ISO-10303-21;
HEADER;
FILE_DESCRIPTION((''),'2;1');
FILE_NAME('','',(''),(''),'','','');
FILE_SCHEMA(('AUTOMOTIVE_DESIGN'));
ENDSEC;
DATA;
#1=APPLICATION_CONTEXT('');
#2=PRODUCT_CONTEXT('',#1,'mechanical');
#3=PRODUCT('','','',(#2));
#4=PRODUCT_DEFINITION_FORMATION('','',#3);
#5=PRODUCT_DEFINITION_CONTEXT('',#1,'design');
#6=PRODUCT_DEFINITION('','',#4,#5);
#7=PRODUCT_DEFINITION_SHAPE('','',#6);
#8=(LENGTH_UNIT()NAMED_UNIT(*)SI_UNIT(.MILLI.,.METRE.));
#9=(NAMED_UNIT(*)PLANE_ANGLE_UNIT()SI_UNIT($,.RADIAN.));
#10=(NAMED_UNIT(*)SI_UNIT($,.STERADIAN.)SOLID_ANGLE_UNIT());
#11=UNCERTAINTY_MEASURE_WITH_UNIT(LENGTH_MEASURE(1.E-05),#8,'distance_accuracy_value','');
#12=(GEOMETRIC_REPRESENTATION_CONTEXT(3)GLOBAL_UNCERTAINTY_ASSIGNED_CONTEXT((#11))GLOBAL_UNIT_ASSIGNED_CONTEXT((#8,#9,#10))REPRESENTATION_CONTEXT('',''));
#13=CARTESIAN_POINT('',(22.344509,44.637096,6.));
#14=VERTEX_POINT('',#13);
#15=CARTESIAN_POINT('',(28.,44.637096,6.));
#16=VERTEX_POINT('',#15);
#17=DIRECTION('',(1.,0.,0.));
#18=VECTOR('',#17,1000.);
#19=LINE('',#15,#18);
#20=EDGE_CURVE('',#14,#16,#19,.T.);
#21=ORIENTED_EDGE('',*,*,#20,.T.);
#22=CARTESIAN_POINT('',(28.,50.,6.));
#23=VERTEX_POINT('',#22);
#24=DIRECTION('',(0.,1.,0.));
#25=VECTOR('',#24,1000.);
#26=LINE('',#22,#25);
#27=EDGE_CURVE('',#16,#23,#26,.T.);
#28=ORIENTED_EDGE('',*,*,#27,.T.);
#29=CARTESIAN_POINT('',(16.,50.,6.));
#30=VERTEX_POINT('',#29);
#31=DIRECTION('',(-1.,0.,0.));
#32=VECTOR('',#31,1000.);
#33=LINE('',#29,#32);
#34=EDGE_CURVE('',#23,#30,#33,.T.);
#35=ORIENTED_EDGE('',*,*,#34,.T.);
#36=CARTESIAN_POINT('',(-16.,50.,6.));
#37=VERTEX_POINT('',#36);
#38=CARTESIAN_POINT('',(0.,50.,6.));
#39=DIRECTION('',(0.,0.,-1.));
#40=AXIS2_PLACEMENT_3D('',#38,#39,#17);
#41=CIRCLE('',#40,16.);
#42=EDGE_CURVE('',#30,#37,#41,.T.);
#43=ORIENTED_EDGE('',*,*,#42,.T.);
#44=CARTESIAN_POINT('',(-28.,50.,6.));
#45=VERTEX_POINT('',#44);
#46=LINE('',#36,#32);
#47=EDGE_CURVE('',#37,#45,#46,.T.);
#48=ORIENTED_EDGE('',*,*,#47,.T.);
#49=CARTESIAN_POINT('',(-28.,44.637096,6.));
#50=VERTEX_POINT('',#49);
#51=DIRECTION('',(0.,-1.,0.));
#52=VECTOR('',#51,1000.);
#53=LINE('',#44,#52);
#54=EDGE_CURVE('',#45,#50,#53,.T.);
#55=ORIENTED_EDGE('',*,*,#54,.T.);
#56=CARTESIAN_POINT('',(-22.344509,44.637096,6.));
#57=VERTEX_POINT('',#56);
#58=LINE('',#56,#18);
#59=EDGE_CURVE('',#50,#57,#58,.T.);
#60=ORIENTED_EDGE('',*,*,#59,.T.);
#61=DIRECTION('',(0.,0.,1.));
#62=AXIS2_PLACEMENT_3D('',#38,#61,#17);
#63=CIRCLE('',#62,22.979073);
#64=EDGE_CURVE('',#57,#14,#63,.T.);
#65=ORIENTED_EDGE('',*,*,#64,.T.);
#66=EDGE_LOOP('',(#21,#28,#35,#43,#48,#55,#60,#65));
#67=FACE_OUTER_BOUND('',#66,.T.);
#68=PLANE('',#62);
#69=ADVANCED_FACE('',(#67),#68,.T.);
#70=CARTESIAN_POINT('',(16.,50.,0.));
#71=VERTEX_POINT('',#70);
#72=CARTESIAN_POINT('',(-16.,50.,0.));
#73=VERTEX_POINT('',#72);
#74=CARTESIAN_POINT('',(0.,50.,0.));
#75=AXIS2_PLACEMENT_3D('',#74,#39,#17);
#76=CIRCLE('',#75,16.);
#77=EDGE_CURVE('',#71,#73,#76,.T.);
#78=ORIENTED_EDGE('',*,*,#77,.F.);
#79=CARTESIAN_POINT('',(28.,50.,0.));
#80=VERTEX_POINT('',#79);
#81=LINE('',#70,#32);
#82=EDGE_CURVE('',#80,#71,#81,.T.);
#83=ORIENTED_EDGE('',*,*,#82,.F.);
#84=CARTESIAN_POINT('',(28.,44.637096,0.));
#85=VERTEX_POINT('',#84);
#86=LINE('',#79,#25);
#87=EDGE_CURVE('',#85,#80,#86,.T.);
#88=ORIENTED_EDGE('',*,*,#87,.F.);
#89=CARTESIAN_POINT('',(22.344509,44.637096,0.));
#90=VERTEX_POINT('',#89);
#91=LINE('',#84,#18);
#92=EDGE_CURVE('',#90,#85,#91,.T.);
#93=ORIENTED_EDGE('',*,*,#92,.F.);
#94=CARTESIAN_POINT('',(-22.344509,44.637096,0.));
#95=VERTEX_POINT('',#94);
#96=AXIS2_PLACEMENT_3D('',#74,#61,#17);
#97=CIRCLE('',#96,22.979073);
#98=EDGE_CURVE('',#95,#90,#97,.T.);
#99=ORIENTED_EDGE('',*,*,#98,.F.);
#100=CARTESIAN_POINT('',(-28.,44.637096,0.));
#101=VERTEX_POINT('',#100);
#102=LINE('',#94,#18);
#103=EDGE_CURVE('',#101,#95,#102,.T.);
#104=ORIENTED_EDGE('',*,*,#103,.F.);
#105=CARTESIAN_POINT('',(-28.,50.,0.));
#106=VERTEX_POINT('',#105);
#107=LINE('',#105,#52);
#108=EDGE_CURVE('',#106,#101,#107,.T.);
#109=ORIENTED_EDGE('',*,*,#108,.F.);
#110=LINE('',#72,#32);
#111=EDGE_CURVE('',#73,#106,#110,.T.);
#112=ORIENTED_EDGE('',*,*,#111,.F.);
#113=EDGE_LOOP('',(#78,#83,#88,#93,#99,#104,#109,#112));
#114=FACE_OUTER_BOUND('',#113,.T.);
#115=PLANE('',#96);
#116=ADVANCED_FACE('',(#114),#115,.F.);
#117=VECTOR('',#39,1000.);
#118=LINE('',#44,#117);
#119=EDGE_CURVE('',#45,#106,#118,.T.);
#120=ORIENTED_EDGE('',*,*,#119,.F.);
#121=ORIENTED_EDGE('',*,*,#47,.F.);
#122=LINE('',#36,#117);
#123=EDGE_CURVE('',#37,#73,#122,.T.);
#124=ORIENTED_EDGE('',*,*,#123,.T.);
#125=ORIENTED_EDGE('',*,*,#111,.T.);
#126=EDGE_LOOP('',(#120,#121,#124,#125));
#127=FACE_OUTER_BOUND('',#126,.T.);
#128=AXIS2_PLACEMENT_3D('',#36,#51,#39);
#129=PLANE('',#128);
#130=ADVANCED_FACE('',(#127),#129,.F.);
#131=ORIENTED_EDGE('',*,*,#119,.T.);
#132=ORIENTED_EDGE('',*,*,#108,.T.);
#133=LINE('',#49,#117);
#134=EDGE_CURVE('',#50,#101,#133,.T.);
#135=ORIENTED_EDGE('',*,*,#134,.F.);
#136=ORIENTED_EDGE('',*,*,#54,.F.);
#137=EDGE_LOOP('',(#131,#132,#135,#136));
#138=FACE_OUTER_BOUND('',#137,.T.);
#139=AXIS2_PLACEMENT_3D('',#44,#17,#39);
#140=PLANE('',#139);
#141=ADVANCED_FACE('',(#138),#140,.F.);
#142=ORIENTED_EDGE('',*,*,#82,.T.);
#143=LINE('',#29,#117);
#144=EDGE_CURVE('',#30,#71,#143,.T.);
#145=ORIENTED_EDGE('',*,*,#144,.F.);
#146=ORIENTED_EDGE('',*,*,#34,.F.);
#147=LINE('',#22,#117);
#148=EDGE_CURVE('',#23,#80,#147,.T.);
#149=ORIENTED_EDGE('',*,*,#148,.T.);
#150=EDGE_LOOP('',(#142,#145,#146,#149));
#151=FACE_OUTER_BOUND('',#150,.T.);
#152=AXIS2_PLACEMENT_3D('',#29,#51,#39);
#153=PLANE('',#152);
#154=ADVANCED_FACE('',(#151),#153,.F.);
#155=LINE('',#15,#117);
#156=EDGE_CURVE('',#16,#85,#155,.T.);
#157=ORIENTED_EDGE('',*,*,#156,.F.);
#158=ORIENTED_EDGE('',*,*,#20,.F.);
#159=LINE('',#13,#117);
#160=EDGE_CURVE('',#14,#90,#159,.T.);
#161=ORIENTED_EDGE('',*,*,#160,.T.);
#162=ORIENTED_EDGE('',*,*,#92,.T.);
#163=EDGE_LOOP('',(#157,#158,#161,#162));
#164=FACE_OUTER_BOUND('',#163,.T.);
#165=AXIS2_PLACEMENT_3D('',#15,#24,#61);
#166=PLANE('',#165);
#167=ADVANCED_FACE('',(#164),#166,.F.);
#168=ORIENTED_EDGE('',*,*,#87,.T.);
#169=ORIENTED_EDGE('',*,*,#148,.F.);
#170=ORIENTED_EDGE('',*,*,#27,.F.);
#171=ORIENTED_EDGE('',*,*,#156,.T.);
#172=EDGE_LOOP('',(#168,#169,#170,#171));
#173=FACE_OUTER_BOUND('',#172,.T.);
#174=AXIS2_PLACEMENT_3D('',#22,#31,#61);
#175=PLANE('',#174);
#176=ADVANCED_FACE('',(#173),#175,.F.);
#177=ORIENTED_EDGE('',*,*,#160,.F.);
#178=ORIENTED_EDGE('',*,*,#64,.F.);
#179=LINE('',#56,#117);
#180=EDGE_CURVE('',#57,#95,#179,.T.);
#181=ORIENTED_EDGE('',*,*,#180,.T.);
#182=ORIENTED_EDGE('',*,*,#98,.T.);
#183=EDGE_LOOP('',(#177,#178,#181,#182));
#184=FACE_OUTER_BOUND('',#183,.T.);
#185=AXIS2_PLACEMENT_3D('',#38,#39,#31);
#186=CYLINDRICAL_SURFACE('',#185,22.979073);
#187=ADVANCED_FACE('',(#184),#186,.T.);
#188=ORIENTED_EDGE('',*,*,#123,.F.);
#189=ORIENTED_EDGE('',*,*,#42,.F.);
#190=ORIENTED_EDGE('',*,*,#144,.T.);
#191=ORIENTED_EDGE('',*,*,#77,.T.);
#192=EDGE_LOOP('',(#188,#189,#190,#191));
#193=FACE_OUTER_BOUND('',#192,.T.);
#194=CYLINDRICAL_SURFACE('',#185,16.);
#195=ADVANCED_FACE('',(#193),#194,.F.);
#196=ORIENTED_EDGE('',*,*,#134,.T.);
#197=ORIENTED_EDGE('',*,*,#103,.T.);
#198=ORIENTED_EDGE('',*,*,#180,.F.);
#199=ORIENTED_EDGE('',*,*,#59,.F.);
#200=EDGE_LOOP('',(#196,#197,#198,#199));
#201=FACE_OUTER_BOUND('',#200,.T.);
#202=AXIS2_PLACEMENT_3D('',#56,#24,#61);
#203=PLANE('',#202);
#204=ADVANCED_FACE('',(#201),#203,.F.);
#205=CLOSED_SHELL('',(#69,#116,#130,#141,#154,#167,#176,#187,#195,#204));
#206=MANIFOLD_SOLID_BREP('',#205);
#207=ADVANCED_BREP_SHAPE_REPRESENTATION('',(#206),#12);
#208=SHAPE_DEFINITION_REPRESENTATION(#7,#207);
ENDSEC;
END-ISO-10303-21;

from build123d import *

# Parameters (mm, degrees)
BOSS_EXTRUDE1_DEPTH = 6


with BuildPart() as part:
    # Sketch1 → Boss-Extrude1 (new body)
    with BuildSketch(Plane.XY):
        with BuildLine():
            Line((-16, 50), (-28, 50))
            Line((-28, 50), (-28, 44.637095603))
            Line((-28, 44.637095603), (-22.344508596, 44.637095603))
            ThreePointArc((-22.344508596, 44.637095603), (0, 27.020926738), (22.344508596, 44.637095603))
            Line((22.344508596, 44.637095603), (28, 44.637095603))
            Line((28, 44.637095603), (28, 50))
            Line((28, 50), (16, 50))
            ThreePointArc((16, 50), (0, 34), (-16, 50))
        make_face()
    extrude(amount=BOSS_EXTRUDE1_DEPTH)


solid = part.part
